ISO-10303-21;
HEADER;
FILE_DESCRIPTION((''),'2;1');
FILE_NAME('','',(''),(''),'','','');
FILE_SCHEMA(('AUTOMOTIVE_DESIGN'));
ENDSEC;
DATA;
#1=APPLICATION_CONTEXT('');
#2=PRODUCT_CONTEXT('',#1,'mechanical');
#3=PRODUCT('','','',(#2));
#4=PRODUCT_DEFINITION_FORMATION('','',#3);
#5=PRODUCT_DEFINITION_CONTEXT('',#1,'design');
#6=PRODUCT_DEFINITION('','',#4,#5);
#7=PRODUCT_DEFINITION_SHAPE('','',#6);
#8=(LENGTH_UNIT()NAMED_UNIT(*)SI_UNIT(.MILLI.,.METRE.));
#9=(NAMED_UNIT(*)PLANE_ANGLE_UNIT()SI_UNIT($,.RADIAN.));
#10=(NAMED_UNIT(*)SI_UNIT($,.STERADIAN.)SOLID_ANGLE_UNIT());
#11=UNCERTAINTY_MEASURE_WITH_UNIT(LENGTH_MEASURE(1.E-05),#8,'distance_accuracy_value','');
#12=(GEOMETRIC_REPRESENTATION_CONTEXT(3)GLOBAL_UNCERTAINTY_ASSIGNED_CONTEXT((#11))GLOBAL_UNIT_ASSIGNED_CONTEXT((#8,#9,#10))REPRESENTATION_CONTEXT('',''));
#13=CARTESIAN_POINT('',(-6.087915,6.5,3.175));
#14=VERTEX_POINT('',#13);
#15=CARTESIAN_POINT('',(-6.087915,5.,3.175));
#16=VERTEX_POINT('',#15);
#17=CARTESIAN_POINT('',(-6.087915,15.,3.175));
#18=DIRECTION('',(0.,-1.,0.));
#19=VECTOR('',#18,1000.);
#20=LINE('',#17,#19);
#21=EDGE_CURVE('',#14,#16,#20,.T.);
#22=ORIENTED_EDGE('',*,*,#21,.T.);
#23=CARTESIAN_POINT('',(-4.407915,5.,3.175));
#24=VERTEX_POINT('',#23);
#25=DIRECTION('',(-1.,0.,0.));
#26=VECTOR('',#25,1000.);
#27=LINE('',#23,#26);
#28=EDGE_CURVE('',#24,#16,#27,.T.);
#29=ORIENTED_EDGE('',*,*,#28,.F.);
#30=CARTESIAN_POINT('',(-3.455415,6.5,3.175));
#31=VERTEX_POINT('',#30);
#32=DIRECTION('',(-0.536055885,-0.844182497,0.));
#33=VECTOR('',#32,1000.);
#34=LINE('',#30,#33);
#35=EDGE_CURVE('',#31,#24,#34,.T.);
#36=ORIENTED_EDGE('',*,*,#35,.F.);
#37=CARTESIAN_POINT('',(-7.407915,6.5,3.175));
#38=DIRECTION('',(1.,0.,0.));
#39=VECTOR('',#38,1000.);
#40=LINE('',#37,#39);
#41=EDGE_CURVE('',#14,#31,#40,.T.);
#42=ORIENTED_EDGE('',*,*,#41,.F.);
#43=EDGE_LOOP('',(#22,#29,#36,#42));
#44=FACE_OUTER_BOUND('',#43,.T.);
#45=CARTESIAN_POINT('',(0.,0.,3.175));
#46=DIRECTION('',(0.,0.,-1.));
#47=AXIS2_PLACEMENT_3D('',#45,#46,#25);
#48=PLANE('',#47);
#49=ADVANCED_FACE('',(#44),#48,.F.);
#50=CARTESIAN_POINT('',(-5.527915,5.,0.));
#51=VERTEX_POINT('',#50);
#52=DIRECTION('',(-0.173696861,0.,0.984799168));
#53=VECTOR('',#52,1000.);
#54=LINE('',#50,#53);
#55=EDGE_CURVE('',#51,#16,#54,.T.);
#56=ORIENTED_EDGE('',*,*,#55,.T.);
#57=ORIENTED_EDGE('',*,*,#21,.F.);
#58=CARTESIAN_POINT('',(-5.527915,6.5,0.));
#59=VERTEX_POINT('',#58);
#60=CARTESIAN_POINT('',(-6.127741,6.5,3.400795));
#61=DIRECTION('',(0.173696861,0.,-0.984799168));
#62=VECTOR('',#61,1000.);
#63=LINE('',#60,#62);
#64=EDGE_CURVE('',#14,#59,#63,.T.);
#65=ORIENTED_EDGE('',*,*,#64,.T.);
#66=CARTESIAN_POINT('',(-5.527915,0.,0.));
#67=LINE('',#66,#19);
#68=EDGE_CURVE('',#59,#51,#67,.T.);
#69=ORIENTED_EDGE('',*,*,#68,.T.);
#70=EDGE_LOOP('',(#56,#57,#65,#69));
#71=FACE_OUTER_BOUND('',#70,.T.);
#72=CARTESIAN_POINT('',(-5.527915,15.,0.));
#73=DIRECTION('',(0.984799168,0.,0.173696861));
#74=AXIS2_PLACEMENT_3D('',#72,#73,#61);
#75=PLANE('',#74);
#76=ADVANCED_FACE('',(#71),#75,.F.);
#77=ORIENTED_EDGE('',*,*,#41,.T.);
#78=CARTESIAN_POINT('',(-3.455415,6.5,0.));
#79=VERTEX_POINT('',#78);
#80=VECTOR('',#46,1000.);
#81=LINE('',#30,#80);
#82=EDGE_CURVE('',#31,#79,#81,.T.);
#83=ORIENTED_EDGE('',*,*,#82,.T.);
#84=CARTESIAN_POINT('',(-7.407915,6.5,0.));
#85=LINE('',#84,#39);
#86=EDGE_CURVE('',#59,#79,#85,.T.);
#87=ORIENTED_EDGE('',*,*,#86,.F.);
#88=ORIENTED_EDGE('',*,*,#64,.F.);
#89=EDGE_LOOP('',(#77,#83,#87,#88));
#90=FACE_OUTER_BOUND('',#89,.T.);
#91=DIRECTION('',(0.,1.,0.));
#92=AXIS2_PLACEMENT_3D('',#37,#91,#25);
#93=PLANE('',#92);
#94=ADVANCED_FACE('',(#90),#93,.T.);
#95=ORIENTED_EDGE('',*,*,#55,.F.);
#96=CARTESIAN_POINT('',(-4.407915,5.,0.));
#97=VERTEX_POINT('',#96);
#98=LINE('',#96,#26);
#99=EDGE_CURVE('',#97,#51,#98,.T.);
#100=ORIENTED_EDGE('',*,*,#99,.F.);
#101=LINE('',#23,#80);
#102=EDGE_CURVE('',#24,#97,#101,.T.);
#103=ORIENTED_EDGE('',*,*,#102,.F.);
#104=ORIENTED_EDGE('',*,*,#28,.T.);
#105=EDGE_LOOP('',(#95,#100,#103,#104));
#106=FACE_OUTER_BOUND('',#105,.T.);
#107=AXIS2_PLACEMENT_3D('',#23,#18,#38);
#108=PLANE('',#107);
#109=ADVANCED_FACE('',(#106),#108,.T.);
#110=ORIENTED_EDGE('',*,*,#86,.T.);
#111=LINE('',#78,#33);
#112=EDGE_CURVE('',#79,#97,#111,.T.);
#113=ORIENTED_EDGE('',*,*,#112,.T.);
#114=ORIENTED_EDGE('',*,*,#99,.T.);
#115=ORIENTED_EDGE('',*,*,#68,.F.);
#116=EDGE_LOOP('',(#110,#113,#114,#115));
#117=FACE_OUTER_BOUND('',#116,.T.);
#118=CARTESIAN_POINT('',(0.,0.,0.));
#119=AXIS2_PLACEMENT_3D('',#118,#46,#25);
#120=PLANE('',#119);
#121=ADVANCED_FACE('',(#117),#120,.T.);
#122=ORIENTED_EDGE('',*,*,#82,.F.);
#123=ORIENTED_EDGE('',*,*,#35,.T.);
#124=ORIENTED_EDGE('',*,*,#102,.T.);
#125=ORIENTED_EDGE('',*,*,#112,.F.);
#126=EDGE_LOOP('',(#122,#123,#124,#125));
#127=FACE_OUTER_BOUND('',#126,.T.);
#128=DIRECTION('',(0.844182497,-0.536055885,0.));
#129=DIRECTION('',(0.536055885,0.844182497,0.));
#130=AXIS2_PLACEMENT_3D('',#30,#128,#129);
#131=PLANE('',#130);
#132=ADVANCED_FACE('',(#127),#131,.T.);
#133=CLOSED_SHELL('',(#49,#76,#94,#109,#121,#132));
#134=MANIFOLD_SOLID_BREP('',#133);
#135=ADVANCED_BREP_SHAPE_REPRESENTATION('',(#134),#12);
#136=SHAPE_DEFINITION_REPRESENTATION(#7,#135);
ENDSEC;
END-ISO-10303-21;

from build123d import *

# Parameters (mm, degrees)
EXTRUDE_1_DEPTH     = 3.175
CUT_EXTRUDE_1_DEPTH = 10


with BuildPart() as part:
    # 草图1 → 凸台-拉伸1 (new body)
    with BuildSketch(Plane.XY):
        Polygon((-4.407915319, 5), (-7.407915319, 5), (-7.407915319, 6.5), (-3.455415319, 6.5), align=None)
    extrude(amount=EXTRUDE_1_DEPTH)

    # 草图2 → 切除-拉伸1 (cut)
    with BuildSketch(Plane.XZ.offset(-5)):
        Polygon((-7.407915319, 0), (-5.527915319, 0), (-6.087915319, 3.175), (-7.407915319, 3.175), align=None)
    extrude(amount=-CUT_EXTRUDE_1_DEPTH, mode=Mode.SUBTRACT)


solid = part.part
